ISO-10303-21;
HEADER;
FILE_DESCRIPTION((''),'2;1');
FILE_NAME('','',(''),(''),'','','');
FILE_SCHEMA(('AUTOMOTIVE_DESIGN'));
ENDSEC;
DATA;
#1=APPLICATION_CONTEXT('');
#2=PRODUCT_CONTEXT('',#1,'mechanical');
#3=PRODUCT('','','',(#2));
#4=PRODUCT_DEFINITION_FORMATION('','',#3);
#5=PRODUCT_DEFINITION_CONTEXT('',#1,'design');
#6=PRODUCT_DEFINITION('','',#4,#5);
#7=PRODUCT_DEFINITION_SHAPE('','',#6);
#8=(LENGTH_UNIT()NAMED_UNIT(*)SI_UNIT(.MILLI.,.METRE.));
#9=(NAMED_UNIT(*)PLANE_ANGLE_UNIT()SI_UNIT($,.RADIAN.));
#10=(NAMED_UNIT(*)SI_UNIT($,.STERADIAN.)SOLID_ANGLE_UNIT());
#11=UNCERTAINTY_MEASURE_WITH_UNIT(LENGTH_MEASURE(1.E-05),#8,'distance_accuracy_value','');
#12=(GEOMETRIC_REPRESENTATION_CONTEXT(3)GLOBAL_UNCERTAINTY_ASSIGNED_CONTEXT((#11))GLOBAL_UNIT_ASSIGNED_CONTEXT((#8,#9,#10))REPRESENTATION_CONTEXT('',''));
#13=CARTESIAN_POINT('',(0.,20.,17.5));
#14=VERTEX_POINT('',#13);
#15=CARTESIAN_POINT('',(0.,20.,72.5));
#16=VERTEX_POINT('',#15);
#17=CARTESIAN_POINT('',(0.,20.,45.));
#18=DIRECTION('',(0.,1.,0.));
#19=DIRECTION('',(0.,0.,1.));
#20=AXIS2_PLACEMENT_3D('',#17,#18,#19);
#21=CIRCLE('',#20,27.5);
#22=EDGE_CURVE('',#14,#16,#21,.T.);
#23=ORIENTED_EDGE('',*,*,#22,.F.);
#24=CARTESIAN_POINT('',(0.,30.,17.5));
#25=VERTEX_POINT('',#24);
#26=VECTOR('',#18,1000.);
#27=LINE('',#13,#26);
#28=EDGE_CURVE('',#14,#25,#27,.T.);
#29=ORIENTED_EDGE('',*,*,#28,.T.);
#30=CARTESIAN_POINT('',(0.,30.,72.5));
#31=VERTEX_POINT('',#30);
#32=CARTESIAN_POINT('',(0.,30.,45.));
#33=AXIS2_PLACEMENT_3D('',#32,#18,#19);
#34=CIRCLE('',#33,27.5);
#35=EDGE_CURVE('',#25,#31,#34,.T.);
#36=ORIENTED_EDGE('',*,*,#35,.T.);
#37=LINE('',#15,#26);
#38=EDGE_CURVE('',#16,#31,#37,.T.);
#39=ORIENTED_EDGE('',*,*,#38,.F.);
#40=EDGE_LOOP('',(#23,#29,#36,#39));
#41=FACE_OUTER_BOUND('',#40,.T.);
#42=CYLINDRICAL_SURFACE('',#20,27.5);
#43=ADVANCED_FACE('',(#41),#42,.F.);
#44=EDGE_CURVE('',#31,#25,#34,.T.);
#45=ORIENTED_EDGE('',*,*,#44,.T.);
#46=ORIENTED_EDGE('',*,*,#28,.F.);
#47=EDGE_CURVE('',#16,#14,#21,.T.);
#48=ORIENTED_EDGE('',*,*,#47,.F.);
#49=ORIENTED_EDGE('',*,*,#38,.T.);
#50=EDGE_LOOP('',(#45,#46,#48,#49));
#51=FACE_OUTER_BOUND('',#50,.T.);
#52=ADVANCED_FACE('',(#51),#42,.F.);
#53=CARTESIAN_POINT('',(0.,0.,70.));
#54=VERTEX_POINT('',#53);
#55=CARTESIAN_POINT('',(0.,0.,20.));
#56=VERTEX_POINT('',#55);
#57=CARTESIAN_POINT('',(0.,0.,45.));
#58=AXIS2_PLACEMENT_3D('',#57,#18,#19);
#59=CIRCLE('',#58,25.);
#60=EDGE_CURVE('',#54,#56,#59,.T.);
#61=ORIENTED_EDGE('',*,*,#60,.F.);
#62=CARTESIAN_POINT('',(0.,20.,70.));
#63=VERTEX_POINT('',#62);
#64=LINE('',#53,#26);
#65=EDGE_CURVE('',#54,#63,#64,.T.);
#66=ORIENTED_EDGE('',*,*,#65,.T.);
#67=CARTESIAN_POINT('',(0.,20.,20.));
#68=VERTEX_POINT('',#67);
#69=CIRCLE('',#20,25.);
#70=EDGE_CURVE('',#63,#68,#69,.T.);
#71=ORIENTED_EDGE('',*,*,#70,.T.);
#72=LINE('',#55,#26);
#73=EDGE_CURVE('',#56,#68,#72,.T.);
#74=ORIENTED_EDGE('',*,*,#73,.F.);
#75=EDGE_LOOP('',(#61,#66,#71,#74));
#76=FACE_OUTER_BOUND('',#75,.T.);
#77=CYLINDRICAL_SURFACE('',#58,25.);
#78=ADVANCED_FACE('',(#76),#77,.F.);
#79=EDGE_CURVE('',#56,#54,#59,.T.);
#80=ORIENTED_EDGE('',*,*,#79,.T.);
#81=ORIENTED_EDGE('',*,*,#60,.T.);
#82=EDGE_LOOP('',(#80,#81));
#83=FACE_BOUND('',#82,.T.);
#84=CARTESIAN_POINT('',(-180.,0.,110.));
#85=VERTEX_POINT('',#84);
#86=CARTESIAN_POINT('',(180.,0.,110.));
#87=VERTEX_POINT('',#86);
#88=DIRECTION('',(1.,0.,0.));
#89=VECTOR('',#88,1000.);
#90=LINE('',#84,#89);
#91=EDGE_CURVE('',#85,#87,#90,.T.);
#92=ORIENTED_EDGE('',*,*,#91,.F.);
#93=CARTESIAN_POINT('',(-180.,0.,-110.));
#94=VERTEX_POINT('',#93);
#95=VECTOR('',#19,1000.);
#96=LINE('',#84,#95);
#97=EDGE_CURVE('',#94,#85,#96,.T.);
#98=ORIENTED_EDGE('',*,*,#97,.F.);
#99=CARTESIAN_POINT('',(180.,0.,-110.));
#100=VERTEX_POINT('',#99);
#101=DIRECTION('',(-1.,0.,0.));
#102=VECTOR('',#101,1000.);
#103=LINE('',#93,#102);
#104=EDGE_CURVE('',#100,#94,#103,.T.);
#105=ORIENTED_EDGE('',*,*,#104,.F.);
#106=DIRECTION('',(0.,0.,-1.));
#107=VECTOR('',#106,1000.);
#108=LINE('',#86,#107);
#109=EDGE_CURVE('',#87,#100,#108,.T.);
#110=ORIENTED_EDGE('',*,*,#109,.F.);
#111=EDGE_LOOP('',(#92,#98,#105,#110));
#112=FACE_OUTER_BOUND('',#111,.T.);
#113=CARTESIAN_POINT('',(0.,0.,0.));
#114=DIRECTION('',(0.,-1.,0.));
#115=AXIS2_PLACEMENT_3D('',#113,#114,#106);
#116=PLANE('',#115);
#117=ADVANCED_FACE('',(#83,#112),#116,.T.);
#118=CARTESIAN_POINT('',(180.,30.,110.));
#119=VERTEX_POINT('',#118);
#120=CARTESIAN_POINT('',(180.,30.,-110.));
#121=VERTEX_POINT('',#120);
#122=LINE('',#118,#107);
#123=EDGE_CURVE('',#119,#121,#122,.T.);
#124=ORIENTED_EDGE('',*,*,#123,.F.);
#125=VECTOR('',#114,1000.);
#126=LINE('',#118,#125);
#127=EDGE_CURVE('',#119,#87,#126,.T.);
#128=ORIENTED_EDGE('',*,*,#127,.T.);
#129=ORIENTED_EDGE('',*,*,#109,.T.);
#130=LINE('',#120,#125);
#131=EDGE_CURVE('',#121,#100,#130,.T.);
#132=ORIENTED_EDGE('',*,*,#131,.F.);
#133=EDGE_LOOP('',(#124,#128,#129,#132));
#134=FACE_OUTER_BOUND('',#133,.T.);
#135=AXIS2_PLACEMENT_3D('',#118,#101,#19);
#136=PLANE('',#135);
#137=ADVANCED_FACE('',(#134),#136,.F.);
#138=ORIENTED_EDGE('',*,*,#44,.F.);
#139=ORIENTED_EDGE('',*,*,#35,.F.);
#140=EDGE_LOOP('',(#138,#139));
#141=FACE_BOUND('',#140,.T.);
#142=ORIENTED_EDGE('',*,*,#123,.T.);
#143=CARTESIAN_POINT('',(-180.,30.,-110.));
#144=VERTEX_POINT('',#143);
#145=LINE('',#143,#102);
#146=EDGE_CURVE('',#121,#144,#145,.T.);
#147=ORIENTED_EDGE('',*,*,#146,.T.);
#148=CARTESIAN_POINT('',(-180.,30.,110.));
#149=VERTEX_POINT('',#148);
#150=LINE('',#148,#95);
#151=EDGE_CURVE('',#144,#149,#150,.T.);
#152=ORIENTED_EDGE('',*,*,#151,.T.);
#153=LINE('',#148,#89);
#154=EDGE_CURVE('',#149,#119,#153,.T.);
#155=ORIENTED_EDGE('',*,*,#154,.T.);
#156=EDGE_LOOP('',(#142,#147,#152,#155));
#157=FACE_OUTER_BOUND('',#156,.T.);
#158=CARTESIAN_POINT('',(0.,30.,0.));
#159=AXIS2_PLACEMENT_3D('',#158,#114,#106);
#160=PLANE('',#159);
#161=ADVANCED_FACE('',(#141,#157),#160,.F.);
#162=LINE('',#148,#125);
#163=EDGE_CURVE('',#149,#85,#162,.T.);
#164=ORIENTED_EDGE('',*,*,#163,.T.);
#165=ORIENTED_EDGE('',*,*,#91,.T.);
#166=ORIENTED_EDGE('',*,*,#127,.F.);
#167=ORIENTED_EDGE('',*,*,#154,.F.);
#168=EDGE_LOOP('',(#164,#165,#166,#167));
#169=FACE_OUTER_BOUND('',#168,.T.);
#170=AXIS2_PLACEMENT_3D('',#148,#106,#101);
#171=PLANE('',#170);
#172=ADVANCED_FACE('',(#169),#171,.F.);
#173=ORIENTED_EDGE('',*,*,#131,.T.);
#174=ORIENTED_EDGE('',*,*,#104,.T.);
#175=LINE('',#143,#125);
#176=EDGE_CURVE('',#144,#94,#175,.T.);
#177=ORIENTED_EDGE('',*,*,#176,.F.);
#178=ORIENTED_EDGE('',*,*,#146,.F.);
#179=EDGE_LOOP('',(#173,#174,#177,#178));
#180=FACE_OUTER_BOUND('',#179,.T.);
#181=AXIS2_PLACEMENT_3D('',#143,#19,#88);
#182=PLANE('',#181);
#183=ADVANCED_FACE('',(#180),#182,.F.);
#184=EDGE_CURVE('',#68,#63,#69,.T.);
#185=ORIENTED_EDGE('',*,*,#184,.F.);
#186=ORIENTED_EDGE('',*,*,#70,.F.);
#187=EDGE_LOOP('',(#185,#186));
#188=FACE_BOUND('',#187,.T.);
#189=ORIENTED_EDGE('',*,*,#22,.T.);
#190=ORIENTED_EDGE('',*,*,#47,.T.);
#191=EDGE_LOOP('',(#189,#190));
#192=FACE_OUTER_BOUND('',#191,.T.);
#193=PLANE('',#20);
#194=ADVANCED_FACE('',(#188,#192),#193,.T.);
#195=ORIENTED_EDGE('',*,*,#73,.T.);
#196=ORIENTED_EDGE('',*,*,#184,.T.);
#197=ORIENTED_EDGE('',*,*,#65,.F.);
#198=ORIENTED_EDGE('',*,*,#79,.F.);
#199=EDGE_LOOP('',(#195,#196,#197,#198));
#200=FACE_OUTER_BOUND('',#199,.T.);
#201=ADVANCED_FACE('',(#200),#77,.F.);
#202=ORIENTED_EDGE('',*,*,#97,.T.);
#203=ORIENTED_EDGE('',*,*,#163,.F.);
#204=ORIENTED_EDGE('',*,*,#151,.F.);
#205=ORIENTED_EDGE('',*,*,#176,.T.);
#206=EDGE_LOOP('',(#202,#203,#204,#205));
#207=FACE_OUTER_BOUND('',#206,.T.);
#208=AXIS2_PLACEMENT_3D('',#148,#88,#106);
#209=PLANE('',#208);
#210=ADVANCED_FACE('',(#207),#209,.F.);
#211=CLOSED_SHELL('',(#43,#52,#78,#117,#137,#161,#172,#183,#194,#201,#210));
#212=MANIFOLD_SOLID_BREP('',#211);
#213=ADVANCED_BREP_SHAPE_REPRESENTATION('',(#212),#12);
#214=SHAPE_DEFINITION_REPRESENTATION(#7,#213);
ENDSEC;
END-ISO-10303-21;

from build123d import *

# Parameters (mm, degrees)
SKETCH_1_W          = 360
SKETCH_1_H          = 220
EXTRUDE_1_DEPTH     = 30
SKETCH_2_R          = 27.5
CUT_EXTRUDE_1_DEPTH = 10
SKETCH_3_R          = 25
CUT_EXTRUDE_2_DEPTH = 214.072757527


with BuildPart() as part:
    # 草图1 → 凸台-拉伸1 (new body)
    with BuildSketch(Plane(origin=(0, 0, 0), x_dir=(1, 0, 0), z_dir=(0, 1, 0))):
        Rectangle(SKETCH_1_W, SKETCH_1_H)
    extrude(amount=EXTRUDE_1_DEPTH)

    # 草图2 → 切除-拉伸1 (cut)
    with BuildSketch(Plane(origin=(0, 30, 0), x_dir=(1, 0, 0), z_dir=(0, 1, 0))):
        with Locations(Location((0, -45, 0), (0, 0, 270))):
            Circle(SKETCH_2_R)
    extrude(amount=-CUT_EXTRUDE_1_DEPTH, mode=Mode.SUBTRACT)

    # 草图3 → 切除-拉伸2 (cut, through all)
    with BuildSketch(Plane(origin=(0, 30, 0), x_dir=(1, 0, 0), z_dir=(0, 1, 0))):
        with Locations(Location((0, -45, 0), (0, 0, 270))):
            Circle(SKETCH_3_R)
    extrude(amount=-CUT_EXTRUDE_2_DEPTH, mode=Mode.SUBTRACT)


solid = part.part
